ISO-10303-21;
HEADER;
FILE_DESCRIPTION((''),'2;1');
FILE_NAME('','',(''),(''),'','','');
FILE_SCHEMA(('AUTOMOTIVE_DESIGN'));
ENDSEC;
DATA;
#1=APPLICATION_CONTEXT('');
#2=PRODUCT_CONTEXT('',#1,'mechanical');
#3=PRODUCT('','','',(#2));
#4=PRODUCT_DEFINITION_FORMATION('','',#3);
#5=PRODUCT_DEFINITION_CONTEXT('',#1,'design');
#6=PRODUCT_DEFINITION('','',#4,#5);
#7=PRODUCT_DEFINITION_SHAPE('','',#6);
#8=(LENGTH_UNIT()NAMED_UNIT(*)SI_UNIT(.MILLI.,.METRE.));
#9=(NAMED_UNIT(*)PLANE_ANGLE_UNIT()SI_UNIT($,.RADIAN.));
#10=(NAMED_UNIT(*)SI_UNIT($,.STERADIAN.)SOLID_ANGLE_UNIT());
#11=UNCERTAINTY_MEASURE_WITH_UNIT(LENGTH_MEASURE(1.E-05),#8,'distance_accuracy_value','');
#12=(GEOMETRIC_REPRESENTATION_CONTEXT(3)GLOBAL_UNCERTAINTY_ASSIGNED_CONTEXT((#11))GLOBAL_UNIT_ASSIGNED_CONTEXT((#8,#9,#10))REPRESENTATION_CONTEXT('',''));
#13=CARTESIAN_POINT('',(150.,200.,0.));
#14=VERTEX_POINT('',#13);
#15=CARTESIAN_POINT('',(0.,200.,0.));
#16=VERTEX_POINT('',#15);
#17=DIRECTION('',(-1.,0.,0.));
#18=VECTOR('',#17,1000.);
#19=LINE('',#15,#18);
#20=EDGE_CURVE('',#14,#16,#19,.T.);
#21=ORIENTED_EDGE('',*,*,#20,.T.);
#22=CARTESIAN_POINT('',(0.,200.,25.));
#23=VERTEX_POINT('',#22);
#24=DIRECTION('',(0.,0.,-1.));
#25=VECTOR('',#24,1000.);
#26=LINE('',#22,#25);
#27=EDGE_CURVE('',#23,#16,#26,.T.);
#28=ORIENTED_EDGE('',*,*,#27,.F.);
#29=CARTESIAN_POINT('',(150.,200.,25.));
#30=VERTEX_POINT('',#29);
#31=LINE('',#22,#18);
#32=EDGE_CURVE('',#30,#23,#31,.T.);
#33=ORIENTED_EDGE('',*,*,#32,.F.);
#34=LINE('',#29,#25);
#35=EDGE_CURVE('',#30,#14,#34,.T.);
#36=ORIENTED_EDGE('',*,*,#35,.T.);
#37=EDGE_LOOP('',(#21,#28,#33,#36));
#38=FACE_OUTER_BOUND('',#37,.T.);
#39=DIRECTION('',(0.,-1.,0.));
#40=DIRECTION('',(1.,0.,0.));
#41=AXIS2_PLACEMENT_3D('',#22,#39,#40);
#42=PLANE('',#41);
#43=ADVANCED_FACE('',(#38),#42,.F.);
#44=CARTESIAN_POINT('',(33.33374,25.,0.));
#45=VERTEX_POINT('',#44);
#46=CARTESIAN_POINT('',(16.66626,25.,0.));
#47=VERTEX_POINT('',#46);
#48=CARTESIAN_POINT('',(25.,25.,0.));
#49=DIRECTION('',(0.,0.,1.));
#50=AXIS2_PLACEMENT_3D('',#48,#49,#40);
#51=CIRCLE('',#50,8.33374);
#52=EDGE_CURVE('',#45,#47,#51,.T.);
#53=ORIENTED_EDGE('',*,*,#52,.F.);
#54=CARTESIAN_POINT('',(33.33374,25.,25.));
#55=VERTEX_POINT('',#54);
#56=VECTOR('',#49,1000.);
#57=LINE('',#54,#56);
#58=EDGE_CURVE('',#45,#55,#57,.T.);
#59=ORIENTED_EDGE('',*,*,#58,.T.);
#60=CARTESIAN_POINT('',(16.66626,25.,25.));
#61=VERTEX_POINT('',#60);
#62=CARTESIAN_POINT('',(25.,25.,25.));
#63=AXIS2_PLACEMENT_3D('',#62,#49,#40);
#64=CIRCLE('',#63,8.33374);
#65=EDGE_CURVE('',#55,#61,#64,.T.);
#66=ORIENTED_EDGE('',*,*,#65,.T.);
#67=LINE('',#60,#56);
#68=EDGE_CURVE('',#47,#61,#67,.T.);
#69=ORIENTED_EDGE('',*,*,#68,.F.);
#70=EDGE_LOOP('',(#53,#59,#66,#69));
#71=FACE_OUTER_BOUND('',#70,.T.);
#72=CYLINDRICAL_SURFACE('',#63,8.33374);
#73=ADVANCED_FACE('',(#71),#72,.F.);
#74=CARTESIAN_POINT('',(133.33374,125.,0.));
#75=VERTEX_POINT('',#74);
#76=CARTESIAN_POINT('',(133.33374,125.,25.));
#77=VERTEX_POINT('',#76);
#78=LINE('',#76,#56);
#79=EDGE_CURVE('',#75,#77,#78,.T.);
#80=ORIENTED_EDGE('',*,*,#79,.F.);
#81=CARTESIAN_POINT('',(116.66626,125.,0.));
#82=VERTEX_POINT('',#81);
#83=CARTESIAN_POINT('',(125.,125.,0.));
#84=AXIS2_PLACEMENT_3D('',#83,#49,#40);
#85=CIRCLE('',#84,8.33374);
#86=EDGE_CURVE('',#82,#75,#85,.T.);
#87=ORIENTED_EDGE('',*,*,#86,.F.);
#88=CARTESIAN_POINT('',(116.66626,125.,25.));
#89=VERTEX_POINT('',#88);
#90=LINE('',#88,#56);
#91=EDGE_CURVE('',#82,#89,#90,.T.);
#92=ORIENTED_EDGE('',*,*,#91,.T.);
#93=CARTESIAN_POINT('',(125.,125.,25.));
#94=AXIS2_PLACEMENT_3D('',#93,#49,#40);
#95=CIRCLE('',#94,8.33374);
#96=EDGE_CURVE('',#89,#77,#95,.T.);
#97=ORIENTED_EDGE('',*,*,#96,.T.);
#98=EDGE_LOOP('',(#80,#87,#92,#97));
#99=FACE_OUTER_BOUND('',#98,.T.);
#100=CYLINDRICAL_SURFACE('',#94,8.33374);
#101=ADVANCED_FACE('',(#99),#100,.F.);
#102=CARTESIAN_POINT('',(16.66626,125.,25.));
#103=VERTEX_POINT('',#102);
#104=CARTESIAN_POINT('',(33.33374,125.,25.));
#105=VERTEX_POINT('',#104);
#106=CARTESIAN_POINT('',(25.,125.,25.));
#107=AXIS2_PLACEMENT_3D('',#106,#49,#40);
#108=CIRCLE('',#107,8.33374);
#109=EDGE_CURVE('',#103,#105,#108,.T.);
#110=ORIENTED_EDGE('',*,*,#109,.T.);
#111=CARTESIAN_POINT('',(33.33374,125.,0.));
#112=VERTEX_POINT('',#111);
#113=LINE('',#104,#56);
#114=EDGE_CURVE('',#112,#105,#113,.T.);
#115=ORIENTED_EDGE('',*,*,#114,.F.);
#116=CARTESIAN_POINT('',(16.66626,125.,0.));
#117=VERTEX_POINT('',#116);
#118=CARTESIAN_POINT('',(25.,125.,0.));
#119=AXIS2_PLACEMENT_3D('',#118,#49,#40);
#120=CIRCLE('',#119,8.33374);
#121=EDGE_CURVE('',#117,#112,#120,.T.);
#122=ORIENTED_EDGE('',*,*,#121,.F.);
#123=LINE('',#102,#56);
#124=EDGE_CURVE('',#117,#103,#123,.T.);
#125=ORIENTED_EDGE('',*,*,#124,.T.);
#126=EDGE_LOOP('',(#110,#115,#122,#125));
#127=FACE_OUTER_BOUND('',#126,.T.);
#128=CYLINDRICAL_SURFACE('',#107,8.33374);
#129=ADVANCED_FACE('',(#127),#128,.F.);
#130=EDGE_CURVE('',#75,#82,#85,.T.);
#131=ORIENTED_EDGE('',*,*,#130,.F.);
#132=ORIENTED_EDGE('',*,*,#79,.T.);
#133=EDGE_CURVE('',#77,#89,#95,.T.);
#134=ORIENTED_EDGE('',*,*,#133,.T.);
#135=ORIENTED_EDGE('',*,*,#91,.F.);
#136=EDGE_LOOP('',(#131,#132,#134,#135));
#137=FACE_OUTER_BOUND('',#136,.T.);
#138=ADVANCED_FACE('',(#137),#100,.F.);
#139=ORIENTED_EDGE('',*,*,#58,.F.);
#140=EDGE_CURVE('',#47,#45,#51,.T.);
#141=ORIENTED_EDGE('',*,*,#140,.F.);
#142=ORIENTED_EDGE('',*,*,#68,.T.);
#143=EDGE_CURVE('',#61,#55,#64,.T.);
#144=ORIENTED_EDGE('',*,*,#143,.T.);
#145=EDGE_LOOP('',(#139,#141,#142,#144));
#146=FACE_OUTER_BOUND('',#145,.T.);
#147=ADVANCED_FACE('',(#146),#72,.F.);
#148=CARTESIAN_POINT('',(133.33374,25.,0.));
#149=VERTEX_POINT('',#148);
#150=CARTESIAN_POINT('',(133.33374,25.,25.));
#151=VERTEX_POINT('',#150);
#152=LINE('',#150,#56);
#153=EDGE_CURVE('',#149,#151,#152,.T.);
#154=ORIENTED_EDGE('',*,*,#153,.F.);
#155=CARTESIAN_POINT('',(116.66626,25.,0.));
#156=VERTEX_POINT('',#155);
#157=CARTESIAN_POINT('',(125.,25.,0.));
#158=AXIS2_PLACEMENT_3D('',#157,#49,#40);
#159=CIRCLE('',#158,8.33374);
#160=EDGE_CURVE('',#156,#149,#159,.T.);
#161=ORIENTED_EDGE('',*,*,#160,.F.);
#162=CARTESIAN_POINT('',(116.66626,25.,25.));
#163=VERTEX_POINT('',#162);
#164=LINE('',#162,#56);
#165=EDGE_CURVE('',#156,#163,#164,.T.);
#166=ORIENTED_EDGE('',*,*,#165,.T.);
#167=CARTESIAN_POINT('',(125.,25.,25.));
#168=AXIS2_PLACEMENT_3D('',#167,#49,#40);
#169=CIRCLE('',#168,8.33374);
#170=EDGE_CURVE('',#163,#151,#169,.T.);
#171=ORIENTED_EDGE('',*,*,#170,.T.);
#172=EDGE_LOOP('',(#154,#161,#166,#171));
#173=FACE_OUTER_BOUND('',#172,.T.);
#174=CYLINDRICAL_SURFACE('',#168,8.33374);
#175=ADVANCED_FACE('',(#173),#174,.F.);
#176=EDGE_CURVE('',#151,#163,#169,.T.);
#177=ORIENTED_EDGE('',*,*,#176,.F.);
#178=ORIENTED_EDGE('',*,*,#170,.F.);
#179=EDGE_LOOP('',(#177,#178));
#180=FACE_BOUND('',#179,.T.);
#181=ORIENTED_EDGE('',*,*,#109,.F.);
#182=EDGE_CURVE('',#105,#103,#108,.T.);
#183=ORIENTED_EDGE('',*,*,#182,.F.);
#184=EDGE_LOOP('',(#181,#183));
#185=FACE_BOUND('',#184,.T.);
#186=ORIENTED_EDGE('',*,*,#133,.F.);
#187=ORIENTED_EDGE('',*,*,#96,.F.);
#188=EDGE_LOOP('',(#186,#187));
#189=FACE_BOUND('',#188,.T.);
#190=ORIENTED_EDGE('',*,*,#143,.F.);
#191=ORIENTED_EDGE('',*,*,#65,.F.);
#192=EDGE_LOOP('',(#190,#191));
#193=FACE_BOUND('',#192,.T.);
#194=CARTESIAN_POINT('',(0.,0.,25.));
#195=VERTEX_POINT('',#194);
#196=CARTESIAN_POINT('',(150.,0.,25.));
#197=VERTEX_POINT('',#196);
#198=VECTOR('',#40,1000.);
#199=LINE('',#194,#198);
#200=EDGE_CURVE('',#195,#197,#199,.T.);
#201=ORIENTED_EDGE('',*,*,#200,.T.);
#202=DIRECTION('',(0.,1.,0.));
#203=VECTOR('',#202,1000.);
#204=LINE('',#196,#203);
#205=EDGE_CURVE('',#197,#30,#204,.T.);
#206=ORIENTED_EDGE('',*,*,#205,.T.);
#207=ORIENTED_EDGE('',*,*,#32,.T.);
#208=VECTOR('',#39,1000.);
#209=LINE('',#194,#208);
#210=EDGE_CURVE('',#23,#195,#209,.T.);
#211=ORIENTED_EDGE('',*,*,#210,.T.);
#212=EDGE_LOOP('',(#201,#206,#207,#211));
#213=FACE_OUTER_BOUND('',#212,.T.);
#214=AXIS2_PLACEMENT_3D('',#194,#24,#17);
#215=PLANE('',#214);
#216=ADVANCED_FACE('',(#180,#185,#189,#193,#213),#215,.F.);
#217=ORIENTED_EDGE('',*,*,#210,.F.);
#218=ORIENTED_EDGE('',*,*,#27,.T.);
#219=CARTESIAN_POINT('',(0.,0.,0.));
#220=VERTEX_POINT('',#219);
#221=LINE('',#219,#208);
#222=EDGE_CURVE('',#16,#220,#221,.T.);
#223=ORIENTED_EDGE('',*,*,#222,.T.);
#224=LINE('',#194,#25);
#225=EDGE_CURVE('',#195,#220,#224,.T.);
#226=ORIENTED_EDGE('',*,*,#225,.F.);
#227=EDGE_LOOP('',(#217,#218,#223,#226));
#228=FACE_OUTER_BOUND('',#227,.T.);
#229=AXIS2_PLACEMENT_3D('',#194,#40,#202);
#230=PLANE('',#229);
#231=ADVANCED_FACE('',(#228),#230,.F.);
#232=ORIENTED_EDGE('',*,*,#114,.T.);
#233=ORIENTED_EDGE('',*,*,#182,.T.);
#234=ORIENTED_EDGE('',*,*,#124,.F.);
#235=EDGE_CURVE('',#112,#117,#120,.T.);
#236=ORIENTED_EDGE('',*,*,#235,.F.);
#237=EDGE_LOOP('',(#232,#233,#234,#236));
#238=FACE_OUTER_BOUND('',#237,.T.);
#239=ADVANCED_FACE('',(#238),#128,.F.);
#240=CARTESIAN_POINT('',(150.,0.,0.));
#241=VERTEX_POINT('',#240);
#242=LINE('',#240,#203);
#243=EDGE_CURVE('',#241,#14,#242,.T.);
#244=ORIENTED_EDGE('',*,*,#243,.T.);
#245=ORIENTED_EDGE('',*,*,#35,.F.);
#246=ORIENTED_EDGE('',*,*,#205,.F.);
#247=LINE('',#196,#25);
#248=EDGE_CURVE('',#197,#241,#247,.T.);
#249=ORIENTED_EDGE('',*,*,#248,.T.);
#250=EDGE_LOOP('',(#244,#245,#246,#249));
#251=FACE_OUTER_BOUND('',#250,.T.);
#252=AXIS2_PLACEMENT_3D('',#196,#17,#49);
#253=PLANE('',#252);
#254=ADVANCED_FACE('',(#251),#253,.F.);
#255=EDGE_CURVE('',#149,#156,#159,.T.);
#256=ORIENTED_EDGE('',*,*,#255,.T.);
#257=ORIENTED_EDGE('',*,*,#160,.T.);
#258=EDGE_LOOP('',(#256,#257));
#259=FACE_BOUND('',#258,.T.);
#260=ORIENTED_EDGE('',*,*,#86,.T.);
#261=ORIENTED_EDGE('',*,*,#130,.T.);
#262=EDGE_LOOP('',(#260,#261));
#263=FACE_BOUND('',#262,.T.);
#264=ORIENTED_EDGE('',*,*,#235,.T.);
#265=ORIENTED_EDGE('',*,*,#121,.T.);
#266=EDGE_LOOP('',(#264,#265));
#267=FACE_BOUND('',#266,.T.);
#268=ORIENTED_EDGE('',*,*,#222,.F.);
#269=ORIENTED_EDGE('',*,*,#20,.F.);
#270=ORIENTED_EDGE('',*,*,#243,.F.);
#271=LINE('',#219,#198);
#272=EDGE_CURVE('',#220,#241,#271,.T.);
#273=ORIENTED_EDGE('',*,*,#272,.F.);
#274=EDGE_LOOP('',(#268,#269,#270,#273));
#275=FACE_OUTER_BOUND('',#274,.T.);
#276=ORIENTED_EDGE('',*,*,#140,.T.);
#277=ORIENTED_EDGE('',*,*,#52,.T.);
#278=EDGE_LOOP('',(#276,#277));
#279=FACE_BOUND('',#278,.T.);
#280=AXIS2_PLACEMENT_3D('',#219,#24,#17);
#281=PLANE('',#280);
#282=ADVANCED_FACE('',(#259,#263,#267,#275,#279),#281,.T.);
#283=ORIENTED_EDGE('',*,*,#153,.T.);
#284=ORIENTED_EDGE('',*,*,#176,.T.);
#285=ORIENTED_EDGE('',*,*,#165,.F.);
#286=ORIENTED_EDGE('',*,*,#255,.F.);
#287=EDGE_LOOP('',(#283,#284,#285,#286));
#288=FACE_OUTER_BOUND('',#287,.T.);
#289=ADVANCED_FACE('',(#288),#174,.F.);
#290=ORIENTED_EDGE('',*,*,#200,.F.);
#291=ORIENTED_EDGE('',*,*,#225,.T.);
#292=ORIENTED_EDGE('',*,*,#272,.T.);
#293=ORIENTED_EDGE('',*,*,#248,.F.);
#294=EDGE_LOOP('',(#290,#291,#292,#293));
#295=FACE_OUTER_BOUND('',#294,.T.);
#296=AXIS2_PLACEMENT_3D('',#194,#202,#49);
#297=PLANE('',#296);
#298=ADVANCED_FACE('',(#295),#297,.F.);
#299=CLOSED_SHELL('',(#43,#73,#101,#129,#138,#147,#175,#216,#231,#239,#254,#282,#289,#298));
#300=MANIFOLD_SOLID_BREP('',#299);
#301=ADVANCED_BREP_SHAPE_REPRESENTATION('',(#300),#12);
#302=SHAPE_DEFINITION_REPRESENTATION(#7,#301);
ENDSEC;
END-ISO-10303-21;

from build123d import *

# Parameters (mm, degrees)
SKETCH1_W                 = 150
SKETCH1_H                 = 200
BOSS_EXTRUDE1_DEPTH       = 25
F_3_4_10_THREADED_HOLE1_D = 16.66748


with BuildPart() as part:
    # Sketch1 → Boss-Extrude1 (new body)
    with BuildSketch(Plane.XY):
        with Locations((75, 100)):
            Rectangle(SKETCH1_W, SKETCH1_H)
    extrude(amount=BOSS_EXTRUDE1_DEPTH)

    # 3/4-10 Threaded hole1 (through all)
    with Locations(Plane(origin=(25, 125, 25), x_dir=(1, 0, 0), z_dir=(0, 0, 1))):
        with Locations((0, 0), (100, 0), (0, -100), (100, -100)):
            Hole(F_3_4_10_THREADED_HOLE1_D / 2)


solid = part.part
